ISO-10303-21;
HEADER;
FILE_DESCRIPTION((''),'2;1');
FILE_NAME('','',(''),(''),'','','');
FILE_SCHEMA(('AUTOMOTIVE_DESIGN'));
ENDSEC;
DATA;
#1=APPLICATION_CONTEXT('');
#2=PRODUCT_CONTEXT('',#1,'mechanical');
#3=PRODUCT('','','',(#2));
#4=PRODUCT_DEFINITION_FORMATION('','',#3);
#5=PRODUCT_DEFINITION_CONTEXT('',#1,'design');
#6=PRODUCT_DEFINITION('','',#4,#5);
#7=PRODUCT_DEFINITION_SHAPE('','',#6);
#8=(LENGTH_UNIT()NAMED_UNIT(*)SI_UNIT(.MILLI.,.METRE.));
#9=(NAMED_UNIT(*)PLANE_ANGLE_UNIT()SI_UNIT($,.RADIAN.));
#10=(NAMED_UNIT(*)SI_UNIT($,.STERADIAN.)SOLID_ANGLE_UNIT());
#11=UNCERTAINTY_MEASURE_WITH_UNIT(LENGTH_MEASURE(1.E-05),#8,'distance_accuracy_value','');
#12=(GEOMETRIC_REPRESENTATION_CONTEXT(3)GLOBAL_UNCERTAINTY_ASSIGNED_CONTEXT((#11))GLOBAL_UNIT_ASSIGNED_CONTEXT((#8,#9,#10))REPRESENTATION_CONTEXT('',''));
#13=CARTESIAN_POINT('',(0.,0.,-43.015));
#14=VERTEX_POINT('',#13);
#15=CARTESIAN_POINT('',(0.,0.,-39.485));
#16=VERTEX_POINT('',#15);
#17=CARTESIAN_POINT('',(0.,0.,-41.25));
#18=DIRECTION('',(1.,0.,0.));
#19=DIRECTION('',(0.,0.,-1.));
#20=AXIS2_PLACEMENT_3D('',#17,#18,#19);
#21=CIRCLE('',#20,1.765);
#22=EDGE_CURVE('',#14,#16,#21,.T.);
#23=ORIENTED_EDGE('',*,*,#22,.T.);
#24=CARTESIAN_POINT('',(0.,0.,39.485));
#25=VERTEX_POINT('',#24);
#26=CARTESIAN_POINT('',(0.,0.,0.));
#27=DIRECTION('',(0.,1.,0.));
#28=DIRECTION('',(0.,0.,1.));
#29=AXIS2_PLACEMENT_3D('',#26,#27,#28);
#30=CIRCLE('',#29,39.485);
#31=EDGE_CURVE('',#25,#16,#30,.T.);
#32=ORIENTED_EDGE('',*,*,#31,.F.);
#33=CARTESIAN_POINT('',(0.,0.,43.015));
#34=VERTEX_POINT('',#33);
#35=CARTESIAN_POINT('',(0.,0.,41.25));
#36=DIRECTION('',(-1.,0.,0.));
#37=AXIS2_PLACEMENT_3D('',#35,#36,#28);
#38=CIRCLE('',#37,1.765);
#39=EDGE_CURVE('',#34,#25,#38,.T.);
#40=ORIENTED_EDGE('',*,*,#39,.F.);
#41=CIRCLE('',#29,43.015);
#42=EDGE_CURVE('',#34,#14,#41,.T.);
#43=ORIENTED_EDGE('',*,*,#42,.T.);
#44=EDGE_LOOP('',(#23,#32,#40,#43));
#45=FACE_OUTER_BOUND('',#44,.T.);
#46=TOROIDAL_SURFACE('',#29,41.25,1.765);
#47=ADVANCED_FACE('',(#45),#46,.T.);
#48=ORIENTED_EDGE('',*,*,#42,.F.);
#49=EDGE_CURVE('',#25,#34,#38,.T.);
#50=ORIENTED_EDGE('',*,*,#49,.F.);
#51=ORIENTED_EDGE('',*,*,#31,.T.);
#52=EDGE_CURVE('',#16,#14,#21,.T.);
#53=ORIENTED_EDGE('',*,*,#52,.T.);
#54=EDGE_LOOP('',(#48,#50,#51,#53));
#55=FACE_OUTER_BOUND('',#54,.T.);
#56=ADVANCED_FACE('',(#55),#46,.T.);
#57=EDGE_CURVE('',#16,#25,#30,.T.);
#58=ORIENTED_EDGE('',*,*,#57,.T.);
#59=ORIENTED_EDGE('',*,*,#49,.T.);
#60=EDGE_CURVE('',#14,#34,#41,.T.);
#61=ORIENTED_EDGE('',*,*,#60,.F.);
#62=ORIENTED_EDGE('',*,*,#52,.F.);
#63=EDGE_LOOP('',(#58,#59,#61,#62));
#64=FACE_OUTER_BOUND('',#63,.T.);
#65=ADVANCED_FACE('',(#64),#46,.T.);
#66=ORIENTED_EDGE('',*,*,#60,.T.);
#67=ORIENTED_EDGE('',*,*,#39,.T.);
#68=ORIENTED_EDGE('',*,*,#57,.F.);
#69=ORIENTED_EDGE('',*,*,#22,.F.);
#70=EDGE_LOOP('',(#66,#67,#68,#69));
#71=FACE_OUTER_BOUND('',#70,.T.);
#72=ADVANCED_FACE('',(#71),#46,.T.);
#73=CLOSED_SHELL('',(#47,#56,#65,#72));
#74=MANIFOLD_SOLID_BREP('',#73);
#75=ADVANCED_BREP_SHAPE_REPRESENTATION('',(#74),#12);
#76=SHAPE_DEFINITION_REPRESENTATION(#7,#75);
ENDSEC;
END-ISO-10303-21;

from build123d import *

# Parameters (mm, degrees)
SKETCH1_R = 1.765


with BuildPart() as part:
    # Sketch1 → Revolve1 (revolve)
    with BuildSketch(Plane.XY, mode=Mode.PRIVATE) as revolve1_sk:
        with Locations((41.25, 0)):
            Circle(SKETCH1_R)
    revolve(revolve1_sk.sketch.rotate(Axis((0, 6.392760857, 0), (0, -1, 0)), 90), axis=Axis((0, 6.392760857, 0), (0, -1, 0)))


solid = part.part
